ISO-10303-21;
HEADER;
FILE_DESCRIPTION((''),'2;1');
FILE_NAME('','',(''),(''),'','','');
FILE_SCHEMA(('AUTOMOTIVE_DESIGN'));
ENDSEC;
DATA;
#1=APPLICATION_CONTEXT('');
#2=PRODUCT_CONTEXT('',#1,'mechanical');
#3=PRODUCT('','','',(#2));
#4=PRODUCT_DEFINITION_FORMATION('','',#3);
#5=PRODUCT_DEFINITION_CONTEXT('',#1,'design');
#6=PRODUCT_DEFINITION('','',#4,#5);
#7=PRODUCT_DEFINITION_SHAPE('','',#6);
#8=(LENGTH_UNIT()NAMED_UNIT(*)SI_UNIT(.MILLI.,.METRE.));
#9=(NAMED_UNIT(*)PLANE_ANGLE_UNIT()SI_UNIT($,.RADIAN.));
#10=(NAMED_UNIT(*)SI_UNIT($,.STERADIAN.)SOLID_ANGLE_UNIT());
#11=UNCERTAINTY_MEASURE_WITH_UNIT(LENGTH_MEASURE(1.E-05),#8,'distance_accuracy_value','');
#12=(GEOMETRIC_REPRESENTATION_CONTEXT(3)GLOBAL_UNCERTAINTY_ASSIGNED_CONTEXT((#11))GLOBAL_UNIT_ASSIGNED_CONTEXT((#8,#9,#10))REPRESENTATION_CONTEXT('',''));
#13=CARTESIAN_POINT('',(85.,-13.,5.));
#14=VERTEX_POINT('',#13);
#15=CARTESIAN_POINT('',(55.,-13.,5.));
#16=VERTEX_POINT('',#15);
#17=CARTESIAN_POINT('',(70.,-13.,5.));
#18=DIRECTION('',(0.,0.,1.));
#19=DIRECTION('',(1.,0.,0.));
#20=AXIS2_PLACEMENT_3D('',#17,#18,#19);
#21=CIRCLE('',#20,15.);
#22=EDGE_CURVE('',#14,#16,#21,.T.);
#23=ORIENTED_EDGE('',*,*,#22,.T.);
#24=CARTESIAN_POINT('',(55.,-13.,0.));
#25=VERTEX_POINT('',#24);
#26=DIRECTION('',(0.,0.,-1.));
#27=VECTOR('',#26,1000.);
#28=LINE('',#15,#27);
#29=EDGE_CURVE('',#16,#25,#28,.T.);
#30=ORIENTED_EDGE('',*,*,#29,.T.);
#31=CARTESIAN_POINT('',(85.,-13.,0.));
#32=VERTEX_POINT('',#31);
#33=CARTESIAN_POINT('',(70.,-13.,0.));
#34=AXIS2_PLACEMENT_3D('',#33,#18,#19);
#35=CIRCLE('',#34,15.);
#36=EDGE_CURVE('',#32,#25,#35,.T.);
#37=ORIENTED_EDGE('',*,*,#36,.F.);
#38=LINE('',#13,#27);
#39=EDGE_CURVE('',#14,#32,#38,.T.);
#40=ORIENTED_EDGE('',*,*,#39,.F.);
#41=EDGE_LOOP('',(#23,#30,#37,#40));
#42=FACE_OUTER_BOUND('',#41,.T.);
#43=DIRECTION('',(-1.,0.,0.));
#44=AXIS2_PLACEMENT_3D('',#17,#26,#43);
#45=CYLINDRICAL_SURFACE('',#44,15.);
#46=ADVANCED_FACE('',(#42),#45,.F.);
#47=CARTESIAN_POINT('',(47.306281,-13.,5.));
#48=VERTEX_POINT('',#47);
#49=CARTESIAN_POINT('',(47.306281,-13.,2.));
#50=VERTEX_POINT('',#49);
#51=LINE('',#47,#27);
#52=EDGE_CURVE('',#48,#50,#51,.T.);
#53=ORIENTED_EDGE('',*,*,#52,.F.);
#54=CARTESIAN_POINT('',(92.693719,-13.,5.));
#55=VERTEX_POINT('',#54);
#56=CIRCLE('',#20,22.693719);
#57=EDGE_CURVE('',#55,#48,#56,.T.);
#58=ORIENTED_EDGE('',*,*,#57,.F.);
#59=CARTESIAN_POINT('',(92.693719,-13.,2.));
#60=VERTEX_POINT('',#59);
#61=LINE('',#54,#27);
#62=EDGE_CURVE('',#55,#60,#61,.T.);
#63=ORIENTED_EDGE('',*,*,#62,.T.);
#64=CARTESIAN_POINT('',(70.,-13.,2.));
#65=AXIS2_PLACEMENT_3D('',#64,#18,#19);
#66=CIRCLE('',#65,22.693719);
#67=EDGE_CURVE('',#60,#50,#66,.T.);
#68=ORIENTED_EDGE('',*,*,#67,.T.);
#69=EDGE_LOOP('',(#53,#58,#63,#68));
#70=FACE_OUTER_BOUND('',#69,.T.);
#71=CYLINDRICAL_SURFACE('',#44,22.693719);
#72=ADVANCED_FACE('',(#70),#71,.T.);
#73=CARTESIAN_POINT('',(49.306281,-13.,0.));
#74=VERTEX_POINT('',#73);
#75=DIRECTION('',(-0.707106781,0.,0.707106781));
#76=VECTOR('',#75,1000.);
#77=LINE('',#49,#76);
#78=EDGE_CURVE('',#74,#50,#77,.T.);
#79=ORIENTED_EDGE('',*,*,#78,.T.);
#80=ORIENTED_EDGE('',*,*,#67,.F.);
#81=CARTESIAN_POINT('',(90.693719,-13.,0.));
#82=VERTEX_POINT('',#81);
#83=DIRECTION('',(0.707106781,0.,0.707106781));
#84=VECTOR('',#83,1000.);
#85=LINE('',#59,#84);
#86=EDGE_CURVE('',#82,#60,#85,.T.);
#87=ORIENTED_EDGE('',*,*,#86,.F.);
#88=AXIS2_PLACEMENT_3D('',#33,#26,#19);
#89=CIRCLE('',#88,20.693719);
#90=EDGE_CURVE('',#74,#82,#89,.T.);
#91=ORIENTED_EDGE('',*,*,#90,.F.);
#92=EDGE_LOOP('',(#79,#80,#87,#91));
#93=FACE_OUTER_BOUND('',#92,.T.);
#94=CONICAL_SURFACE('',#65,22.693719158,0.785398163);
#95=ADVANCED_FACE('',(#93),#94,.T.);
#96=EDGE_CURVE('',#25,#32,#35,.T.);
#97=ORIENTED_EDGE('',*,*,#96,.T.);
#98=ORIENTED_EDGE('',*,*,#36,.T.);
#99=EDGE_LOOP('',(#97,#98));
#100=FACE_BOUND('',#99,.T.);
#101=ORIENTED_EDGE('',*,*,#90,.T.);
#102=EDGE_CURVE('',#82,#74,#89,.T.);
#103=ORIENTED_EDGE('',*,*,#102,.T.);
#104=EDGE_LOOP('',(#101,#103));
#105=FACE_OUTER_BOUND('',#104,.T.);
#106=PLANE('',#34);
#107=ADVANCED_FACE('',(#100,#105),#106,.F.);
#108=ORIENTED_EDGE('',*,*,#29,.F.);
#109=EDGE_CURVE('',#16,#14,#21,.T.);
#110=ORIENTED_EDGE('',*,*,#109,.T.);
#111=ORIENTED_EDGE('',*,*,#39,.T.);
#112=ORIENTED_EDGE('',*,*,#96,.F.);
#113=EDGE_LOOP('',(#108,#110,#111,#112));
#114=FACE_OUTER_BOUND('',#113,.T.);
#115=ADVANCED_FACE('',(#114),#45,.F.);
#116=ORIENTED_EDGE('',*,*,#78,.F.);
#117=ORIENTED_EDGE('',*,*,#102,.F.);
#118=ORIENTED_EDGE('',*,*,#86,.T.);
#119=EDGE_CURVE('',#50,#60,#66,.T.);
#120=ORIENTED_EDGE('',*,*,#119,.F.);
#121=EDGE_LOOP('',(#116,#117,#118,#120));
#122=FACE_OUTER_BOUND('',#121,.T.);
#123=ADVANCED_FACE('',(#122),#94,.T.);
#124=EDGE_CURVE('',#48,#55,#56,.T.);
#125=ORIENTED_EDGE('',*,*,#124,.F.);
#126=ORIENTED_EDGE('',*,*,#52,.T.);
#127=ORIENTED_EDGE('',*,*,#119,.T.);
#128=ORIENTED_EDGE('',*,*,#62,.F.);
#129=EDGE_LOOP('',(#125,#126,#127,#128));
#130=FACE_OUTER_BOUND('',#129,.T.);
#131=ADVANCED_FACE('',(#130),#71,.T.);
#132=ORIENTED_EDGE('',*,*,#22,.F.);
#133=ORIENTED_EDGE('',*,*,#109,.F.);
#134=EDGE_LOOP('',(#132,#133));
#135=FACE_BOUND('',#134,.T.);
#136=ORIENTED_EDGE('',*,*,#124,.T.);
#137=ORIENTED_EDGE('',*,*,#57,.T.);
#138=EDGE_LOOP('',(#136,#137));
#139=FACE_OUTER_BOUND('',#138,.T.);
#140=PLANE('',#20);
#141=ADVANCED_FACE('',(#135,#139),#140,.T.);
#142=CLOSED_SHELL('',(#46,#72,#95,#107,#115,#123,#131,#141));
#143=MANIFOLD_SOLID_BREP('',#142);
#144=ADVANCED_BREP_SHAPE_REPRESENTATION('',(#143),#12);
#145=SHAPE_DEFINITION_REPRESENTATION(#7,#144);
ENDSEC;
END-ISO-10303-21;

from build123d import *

# Parameters (mm, degrees)
SKETCH2_R           = 22.693719158
SKETCH2_R_2         = 15
BOSS_EXTRUDE1_DEPTH = 5
CHAMFER1_SIZE       = 2


with BuildPart() as part:
    # Sketch2 → Boss-Extrude1 (new body)
    with BuildSketch(Plane.XY):
        with Locations((70, -13)):
            Circle(SKETCH2_R)
        with Locations((70, -13)):
            Circle(SKETCH2_R_2, mode=Mode.SUBTRACT)
    extrude(amount=BOSS_EXTRUDE1_DEPTH)

    # Chamfer1
    chamfer1_edges = [part.edges().sort_by_distance(p)[0] for p in [
        (47.306280842, -13, 0),
    ]]
    chamfer(chamfer1_edges, length=CHAMFER1_SIZE)


solid = part.part
